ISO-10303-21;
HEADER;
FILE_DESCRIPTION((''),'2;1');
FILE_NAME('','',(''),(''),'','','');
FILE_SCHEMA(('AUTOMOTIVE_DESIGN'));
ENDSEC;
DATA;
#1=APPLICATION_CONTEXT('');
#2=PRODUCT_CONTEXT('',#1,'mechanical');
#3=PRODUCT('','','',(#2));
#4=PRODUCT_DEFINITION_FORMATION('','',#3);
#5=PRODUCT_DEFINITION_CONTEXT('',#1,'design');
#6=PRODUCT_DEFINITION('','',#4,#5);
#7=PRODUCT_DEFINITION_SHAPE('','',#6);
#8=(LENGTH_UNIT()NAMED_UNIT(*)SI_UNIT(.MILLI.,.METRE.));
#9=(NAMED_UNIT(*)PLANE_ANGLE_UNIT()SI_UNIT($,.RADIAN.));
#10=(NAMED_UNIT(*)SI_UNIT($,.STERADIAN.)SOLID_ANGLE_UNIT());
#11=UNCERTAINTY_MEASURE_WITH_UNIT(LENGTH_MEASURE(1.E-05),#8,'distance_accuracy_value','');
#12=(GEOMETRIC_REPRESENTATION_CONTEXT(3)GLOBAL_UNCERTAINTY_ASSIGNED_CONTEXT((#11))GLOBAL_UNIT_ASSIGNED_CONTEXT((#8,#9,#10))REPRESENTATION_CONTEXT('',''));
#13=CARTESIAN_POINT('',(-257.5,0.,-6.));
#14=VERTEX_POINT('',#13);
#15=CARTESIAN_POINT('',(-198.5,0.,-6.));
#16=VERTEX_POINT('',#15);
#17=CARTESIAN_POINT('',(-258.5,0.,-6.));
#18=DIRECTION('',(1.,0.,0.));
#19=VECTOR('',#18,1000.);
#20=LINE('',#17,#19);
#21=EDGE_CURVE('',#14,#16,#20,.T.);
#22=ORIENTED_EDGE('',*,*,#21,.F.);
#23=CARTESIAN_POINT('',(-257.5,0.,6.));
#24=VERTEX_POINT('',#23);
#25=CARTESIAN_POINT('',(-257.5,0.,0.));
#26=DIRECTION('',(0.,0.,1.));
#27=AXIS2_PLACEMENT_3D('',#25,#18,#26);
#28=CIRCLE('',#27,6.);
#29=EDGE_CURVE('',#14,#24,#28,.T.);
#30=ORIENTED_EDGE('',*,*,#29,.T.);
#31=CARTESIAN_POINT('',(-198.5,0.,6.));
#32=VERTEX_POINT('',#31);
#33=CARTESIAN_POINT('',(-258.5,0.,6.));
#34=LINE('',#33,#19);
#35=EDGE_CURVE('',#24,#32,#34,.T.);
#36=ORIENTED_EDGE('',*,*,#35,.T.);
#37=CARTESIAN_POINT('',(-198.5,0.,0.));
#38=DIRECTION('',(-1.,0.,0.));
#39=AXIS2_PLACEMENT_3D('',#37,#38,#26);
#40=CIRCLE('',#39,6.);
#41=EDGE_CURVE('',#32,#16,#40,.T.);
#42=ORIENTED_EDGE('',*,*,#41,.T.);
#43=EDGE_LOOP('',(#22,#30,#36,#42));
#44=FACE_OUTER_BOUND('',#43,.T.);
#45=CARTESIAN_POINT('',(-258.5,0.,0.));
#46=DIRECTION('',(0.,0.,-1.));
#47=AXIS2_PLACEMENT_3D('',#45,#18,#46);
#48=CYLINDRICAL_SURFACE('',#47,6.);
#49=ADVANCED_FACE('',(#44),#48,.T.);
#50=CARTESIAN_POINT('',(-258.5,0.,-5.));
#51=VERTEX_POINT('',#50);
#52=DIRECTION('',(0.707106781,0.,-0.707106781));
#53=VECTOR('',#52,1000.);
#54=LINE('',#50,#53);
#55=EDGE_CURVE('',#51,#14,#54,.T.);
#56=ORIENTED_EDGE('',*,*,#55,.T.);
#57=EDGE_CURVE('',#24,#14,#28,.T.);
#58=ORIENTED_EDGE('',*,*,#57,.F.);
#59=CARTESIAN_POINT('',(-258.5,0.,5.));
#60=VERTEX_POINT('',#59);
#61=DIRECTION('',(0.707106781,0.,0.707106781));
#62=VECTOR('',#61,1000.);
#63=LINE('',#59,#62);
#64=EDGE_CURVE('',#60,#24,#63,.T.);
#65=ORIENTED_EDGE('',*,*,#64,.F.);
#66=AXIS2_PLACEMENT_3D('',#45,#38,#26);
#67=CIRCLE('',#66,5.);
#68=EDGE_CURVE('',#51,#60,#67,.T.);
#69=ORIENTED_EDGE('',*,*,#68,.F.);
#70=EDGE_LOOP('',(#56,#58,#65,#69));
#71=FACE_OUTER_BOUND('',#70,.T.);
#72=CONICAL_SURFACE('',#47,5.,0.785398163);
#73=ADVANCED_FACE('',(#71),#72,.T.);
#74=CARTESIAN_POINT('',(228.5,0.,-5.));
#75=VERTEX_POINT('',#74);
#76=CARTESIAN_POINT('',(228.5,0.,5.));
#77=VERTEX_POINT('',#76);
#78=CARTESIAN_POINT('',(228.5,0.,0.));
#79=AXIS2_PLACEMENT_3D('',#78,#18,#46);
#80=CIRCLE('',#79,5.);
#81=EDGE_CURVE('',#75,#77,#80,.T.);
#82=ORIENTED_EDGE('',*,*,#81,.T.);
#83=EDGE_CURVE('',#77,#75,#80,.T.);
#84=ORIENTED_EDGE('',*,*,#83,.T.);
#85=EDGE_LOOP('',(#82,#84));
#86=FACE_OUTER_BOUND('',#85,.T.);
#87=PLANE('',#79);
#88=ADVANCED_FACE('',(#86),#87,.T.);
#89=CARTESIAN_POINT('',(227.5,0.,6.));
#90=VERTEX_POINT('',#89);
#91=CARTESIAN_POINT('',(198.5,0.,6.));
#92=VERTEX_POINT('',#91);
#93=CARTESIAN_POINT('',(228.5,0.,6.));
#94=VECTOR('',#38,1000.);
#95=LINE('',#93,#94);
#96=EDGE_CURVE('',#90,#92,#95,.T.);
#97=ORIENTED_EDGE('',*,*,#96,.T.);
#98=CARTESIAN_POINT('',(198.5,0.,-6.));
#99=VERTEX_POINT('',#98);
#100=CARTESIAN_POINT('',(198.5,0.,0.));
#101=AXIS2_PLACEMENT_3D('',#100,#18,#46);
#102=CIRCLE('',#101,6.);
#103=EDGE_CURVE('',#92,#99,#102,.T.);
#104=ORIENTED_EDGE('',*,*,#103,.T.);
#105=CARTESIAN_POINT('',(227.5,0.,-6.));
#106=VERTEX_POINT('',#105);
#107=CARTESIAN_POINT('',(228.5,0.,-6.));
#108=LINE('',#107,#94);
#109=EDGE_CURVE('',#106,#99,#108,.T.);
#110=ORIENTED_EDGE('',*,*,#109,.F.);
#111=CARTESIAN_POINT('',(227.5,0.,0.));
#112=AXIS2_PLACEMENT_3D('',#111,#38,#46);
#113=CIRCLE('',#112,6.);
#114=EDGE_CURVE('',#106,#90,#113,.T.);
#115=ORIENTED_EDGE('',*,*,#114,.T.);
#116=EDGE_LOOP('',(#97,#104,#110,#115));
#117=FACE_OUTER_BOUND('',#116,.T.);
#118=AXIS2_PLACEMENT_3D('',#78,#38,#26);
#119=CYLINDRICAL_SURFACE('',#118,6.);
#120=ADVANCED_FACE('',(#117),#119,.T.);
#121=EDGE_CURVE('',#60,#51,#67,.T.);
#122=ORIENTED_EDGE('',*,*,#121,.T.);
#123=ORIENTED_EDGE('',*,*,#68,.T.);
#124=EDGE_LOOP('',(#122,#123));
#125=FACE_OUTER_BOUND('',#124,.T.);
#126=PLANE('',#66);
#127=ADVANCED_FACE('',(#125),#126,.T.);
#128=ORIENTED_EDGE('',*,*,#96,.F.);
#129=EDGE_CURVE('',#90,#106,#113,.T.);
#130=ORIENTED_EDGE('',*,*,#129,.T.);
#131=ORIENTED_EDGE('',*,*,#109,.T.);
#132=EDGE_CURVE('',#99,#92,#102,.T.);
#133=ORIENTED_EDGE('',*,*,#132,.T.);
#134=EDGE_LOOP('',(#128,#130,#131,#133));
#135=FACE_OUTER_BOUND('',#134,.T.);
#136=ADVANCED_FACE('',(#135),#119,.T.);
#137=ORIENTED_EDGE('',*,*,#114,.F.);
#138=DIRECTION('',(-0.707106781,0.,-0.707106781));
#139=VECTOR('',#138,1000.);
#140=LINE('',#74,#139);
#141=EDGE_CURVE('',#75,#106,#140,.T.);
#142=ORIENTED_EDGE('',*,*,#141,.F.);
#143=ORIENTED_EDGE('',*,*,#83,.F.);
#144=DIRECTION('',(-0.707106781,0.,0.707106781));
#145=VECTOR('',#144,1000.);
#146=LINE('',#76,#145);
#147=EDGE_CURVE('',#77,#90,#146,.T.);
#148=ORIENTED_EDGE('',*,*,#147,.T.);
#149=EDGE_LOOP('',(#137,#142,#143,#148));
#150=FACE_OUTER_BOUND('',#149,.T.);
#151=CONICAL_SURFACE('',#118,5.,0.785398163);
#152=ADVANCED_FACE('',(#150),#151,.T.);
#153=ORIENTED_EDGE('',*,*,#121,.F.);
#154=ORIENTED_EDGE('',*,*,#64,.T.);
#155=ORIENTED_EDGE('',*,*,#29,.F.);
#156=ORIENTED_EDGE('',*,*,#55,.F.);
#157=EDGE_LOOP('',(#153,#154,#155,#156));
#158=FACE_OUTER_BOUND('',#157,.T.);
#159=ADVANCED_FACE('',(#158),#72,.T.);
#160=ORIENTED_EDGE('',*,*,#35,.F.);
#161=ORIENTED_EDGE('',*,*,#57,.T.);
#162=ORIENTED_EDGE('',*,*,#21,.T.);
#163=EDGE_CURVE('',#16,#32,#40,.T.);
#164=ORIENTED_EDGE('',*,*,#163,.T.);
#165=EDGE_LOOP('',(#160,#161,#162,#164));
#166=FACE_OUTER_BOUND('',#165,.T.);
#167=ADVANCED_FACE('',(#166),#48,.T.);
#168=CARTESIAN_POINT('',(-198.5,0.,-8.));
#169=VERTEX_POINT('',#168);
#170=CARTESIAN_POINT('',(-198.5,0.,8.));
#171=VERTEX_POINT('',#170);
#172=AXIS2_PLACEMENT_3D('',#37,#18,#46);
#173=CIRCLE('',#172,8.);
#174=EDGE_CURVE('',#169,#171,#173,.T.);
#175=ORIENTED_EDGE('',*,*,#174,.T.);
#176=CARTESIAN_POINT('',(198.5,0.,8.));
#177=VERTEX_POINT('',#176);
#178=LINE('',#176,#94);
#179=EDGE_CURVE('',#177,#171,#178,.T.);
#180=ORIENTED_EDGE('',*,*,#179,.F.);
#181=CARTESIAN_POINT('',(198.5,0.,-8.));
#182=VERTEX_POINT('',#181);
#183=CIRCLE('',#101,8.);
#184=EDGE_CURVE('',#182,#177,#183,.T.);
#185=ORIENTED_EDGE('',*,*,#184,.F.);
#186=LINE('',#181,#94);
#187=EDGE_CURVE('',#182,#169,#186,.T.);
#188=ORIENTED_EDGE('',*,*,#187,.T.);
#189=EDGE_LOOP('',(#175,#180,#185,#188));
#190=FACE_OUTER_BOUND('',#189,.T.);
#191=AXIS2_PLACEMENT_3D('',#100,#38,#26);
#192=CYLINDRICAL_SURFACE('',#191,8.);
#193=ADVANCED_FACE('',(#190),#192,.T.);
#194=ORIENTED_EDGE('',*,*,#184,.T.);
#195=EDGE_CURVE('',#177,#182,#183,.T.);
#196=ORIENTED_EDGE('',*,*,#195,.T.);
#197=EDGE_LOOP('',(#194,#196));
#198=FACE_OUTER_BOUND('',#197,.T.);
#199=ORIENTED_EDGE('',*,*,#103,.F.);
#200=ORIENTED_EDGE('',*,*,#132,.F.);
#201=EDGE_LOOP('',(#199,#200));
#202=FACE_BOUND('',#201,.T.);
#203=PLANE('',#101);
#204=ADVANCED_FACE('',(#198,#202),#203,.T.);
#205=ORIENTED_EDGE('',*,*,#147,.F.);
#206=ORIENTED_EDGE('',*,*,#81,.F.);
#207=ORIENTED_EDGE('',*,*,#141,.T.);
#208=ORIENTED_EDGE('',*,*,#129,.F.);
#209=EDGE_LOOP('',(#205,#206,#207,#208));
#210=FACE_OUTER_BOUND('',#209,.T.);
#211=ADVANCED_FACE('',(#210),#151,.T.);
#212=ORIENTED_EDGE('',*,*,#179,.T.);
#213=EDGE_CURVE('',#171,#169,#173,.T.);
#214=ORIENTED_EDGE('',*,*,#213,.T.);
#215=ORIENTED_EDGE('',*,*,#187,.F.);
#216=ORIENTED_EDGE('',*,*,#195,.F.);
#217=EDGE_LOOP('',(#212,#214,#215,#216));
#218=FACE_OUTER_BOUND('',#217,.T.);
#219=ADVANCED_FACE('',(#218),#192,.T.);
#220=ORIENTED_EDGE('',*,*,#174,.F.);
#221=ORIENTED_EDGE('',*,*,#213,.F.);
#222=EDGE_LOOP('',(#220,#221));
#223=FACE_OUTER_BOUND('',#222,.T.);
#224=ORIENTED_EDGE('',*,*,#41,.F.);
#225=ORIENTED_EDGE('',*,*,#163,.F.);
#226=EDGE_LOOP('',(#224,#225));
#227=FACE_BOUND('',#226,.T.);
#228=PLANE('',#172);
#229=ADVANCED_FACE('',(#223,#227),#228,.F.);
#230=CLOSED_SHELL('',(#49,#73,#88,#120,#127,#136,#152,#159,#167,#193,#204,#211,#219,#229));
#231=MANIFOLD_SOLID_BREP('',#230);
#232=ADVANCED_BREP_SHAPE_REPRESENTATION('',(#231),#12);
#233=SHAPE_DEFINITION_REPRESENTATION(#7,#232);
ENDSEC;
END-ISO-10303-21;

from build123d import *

# Parameters (mm, degrees)
SKETCH1_R           = 8
BOSS_EXTRUDE1_DEPTH = 198.5
SKETCH2_R           = 6
BOSS_EXTRUDE2_DEPTH = 30
BOSS_EXTRUDE3_START = 60
SKETCH3_R           = 6
BOSS_EXTRUDE3_DEPTH = 60
CHAMFER1_SIZE       = 1
CHAMFER2_SIZE       = 1


with BuildPart() as part:
    # Sketch1 → Boss-Extrude1 (new, symmetric)
    with BuildSketch(Plane(origin=(0, 0, 0), x_dir=(0, 0, -1), z_dir=(1, 0, 0))):
        Circle(SKETCH1_R)
    extrude(amount=BOSS_EXTRUDE1_DEPTH, both=True)

    # Sketch2 → Boss-Extrude2 (add)
    with BuildSketch(Plane(origin=(198.5, 0, 0), x_dir=(0, 0, -1), z_dir=(1, 0, 0))):
        Circle(SKETCH2_R)
    extrude(amount=BOSS_EXTRUDE2_DEPTH)

    # Sketch3 → Boss-Extrude3 (add)
    with BuildSketch(Plane.ZY.offset(198.5).offset(BOSS_EXTRUDE3_START)):
        with Locations(Location((0, 0, 0), (0, 0, 180))):
            Circle(SKETCH3_R)
    extrude(amount=-BOSS_EXTRUDE3_DEPTH)

    # Chamfer1
    chamfer1_edges = [part.edges().sort_by_distance(p)[0] for p in [
        (228.5, 0, 6),
    ]]
    chamfer(chamfer1_edges, length=CHAMFER1_SIZE)

    # Chamfer2
    chamfer2_edges = [part.edges().sort_by_distance(p)[0] for p in [
        (-258.5, 0, 6),
    ]]
    chamfer(chamfer2_edges, length=CHAMFER2_SIZE)


solid = part.part
